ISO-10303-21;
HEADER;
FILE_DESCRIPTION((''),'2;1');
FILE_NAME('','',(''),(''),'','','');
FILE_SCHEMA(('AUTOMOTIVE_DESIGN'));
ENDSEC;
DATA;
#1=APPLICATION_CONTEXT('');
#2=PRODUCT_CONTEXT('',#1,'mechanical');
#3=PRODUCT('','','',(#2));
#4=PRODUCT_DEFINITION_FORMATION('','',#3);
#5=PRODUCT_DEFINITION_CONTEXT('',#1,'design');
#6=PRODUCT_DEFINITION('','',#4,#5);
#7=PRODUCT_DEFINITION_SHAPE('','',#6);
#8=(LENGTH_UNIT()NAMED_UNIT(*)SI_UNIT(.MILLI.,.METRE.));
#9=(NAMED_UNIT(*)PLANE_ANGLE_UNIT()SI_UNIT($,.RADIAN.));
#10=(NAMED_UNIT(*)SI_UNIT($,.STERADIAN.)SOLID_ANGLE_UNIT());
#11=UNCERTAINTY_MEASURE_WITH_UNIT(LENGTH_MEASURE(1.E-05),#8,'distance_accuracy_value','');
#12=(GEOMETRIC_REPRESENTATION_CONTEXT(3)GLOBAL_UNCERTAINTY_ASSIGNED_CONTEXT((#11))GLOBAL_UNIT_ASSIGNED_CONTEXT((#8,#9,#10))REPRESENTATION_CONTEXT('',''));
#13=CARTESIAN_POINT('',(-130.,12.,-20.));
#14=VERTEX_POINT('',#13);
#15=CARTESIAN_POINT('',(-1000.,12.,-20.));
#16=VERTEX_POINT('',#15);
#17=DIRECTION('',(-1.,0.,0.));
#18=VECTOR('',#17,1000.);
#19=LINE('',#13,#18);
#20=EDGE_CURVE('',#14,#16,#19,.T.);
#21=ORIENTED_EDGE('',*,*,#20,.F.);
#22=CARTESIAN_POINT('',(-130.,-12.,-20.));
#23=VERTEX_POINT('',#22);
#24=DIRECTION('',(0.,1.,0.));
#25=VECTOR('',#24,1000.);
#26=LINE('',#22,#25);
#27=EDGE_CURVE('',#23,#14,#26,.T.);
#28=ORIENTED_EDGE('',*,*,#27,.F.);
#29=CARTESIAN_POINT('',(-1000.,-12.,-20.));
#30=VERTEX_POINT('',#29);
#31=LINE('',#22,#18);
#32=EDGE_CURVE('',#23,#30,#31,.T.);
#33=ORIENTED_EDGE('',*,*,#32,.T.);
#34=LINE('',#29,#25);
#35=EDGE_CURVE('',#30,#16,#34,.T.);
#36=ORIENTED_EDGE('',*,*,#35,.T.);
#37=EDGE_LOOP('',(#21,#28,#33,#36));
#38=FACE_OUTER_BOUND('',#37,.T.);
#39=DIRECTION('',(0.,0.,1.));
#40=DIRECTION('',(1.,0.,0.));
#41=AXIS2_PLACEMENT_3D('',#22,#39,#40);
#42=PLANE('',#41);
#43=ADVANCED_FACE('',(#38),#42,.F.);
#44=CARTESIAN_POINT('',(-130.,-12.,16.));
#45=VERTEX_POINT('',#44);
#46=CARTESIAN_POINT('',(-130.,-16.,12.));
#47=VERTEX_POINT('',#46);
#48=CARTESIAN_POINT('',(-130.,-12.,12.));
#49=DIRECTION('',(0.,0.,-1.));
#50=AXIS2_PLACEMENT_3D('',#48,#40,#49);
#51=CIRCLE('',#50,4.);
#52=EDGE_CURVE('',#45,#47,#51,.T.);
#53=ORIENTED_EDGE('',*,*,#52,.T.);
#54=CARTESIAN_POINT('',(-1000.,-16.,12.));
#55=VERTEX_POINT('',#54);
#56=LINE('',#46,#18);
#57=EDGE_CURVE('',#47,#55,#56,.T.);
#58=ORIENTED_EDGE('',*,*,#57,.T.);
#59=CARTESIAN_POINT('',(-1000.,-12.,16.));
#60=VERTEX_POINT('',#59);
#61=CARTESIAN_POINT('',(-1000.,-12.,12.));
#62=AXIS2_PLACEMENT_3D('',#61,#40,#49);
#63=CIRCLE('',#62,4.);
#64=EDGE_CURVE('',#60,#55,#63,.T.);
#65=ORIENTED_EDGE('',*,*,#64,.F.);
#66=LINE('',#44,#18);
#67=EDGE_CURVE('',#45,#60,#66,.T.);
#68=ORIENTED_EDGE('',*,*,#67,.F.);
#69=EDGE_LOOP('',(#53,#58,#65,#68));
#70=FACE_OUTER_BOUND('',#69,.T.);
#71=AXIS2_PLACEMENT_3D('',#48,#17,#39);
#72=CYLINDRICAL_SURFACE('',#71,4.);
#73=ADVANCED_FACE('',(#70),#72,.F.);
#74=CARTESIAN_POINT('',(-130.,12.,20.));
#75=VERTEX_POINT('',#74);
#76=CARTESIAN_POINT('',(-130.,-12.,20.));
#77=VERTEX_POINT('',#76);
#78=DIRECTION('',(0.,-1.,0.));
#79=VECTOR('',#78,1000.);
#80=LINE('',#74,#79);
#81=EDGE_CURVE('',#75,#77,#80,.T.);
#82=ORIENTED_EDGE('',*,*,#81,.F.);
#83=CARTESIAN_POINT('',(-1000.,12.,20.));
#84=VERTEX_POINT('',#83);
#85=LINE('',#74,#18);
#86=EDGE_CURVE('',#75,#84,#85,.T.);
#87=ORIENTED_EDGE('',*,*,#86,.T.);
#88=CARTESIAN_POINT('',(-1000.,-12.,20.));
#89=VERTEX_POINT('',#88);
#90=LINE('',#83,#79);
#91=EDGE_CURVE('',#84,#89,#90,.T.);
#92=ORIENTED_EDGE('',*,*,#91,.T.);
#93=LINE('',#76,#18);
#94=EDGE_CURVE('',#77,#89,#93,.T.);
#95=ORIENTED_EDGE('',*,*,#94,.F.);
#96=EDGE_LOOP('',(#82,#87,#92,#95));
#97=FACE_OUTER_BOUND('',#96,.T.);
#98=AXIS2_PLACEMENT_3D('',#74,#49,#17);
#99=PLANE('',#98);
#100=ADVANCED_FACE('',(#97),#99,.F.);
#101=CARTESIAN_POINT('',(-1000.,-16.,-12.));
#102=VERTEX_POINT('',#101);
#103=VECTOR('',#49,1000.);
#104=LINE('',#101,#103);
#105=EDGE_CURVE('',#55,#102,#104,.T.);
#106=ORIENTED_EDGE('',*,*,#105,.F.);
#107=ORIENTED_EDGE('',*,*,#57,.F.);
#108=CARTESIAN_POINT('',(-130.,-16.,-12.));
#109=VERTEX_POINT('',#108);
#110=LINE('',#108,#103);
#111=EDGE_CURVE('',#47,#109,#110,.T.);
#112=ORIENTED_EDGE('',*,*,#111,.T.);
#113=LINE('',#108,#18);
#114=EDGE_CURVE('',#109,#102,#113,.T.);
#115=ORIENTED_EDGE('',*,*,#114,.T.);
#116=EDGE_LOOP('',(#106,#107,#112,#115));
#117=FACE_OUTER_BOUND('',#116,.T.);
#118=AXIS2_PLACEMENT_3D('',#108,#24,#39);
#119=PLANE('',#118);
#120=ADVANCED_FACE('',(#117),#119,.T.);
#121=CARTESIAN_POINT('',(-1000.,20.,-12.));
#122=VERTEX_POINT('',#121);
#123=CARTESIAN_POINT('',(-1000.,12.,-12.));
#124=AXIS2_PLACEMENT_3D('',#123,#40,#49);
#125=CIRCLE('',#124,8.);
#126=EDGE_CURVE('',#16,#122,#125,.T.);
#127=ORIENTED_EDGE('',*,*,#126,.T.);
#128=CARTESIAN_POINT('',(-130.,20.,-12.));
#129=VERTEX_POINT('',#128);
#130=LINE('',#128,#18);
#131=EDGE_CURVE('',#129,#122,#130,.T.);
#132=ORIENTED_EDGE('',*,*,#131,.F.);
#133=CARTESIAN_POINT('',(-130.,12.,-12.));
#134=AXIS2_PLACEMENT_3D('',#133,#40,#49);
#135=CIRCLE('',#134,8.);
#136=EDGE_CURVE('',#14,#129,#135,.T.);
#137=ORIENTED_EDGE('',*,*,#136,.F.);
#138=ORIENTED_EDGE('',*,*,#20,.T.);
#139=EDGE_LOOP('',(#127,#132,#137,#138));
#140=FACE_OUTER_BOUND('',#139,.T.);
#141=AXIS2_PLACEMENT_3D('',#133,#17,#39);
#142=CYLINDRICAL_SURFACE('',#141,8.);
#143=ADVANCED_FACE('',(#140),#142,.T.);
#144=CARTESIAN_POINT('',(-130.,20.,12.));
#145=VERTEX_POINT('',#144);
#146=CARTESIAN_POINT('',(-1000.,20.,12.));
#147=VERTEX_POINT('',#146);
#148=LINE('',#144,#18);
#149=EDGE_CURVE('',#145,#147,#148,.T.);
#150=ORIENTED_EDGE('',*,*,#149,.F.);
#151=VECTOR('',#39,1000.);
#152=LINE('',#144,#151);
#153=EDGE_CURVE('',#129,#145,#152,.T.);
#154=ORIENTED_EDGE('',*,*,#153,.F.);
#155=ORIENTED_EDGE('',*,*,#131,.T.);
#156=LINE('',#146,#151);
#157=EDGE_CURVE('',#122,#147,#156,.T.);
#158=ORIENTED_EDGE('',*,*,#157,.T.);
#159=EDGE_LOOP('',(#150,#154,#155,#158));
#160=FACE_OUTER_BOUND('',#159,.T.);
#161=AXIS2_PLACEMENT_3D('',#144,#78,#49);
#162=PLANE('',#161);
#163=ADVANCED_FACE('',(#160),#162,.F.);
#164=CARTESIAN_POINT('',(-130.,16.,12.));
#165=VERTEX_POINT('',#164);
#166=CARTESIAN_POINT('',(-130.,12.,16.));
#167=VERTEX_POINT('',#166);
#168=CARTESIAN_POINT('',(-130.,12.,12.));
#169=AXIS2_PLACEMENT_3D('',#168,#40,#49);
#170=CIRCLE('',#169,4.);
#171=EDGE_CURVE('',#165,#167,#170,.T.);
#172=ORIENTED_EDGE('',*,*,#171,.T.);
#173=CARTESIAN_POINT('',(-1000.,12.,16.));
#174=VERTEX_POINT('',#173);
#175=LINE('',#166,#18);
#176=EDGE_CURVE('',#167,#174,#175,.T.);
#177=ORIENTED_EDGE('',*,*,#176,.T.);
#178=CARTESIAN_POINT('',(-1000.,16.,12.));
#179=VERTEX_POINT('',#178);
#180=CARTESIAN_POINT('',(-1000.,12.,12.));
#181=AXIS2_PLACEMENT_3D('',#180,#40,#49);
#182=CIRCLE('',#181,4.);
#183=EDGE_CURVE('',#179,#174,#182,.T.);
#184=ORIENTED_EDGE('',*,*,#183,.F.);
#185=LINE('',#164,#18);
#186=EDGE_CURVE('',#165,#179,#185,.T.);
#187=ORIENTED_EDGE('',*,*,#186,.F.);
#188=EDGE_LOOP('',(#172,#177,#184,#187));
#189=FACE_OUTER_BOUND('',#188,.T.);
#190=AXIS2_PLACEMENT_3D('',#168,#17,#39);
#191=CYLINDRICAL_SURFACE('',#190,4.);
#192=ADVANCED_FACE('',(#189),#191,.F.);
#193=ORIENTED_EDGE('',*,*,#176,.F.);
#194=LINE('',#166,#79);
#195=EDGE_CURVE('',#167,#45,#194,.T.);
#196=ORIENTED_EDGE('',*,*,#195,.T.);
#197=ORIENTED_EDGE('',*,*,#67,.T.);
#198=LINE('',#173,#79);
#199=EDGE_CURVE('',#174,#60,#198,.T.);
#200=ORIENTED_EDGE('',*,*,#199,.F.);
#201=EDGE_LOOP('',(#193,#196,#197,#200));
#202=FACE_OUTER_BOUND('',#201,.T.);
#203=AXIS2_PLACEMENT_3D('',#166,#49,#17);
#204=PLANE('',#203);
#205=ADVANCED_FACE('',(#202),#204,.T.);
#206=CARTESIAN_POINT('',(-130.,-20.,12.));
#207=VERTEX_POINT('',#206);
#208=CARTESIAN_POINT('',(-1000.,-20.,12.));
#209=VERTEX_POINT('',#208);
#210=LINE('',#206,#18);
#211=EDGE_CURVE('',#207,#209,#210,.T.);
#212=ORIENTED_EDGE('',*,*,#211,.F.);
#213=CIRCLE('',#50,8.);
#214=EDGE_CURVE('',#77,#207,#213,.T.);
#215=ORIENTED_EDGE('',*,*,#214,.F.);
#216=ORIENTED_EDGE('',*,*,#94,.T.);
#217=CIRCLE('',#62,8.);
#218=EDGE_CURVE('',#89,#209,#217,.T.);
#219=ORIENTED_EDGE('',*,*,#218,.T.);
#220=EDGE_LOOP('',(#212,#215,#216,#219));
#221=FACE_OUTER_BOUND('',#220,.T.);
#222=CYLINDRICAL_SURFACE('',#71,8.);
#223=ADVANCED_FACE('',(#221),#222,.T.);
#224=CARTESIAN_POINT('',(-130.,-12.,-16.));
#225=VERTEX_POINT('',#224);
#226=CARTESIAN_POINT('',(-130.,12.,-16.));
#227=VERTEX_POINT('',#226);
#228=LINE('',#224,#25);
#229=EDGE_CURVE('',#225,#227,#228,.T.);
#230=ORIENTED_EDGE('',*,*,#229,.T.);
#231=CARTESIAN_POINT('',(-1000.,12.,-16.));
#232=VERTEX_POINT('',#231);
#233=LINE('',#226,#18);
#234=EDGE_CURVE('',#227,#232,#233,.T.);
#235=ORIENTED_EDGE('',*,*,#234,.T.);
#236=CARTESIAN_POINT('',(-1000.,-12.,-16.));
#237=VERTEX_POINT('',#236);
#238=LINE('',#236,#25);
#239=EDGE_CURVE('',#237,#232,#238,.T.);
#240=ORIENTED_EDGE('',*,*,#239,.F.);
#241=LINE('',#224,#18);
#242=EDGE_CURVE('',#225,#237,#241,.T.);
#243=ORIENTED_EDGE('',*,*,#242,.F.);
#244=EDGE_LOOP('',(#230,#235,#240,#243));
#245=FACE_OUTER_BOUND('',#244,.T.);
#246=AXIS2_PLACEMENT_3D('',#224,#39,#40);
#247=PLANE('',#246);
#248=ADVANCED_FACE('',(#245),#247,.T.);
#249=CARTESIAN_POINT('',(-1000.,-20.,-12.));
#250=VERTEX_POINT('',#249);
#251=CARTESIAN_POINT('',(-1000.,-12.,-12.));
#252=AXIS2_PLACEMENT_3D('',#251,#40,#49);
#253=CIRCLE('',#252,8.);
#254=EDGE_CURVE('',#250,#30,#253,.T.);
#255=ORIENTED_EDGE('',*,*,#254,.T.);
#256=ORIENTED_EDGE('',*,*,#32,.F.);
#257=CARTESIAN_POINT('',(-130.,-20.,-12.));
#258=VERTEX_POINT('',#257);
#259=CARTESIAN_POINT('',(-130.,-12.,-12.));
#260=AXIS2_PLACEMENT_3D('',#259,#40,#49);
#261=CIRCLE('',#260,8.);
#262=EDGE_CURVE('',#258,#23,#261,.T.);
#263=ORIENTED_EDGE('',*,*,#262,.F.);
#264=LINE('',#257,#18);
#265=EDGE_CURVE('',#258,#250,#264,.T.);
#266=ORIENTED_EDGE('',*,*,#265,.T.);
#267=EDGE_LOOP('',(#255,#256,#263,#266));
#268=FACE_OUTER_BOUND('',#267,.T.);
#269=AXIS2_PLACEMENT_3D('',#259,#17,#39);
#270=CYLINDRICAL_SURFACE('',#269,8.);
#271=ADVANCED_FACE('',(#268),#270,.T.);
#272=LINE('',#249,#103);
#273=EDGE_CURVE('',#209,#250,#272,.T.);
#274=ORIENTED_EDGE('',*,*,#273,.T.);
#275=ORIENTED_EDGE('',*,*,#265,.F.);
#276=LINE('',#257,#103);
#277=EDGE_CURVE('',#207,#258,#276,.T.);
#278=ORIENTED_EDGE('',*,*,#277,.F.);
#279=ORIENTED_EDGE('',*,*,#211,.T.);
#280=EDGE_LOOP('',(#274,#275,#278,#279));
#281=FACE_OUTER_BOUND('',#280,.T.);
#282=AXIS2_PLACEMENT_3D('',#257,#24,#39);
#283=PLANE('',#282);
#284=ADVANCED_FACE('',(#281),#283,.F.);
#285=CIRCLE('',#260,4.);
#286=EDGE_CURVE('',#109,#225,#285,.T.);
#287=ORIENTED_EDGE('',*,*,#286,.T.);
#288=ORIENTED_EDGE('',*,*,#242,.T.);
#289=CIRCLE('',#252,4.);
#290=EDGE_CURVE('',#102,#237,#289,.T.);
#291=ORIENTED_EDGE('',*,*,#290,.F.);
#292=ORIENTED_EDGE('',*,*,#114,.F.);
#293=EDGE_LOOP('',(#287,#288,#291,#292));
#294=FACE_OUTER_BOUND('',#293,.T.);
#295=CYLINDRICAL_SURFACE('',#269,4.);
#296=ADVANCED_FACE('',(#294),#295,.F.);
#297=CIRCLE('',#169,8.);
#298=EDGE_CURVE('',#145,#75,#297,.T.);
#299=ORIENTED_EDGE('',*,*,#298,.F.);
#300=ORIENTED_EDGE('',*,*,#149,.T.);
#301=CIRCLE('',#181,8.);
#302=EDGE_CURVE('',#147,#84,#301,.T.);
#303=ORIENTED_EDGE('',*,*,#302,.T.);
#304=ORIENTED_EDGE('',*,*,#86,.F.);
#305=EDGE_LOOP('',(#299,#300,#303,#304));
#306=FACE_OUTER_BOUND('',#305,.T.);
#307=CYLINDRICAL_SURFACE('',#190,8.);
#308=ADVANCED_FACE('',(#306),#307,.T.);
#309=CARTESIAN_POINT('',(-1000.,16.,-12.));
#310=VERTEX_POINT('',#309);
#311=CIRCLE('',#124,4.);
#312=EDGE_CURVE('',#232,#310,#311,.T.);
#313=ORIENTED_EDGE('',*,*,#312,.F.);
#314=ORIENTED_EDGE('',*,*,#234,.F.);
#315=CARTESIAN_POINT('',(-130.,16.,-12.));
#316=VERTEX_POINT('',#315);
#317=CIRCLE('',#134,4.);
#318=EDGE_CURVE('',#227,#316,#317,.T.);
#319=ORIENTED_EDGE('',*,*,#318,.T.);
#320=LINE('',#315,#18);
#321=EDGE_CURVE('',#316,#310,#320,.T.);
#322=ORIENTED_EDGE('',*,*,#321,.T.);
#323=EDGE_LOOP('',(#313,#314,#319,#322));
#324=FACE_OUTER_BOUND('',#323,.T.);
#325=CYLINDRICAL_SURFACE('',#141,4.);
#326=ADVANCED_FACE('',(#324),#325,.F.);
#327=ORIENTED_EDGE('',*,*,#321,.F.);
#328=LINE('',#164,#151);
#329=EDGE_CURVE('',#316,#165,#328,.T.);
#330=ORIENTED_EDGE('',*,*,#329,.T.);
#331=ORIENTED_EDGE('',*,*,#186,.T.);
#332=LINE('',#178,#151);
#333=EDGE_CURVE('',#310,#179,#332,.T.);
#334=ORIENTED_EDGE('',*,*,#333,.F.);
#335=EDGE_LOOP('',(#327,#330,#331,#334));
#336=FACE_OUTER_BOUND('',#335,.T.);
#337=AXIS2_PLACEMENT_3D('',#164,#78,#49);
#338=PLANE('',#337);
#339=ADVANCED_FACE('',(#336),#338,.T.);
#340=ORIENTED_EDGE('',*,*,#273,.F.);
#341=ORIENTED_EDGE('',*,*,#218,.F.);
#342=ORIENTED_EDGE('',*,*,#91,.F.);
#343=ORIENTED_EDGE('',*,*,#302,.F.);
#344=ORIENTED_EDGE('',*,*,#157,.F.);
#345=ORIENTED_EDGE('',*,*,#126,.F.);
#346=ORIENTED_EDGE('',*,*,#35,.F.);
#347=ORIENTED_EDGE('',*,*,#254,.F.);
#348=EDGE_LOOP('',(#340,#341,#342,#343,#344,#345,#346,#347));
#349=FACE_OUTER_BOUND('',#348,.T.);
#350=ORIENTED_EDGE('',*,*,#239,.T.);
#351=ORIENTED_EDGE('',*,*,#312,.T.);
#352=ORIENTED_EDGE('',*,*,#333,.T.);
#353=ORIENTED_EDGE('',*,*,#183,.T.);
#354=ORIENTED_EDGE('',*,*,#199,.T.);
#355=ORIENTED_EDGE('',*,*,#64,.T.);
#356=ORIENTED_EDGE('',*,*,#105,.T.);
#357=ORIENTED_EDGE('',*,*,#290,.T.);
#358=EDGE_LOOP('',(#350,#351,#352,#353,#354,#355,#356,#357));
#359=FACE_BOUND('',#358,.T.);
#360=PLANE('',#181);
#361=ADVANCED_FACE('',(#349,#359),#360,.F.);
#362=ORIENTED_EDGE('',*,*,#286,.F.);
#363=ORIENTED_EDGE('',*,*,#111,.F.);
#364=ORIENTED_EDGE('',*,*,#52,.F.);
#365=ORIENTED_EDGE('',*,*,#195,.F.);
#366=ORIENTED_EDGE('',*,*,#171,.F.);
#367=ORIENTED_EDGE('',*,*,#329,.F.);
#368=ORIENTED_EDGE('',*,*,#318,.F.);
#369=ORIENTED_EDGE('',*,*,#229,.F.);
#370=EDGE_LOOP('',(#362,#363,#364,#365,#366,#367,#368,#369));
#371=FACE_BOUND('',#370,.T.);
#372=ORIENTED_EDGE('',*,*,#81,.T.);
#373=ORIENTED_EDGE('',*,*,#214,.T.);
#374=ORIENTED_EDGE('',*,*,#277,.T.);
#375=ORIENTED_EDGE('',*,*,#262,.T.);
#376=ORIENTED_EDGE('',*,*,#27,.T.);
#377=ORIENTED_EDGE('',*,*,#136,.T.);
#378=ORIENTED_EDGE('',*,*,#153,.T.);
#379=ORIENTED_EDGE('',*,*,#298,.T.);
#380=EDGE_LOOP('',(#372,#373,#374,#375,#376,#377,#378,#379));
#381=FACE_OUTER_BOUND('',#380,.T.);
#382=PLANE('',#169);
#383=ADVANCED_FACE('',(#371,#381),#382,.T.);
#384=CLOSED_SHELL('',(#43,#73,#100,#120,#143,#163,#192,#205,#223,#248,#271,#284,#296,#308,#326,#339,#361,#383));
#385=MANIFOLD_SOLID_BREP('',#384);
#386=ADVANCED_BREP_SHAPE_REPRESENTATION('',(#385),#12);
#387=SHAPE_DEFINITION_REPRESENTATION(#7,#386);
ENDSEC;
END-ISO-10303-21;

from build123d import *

# Parameters (mm, degrees)
SQUARE_TUBE_40_X_40_X_4_1_DEPTH = 870


with BuildPart() as part:
    # Sketch1 → Square Tube 40 X 40 X 4(1) (new body)
    with BuildSketch(Plane.YZ.offset(-1000)):
        with BuildLine():
            Line((-12, -20), (12, -20))
            ThreePointArc((12, -20), (17.656854249, -17.656854249), (20, -12))
            Line((20, -12), (20, 12))
            ThreePointArc((20, 12), (17.656854249, 17.656854249), (12, 20))
            Line((12, 20), (-12, 20))
            ThreePointArc((-12, 20), (-17.656854249, 17.656854249), (-20, 12))
            Line((-20, 12), (-20, -12))
            ThreePointArc((-20, -12), (-17.656854249, -17.656854249), (-12, -20))
        make_face()
        with BuildLine():
            Line((-12, -16), (12, -16))
            ThreePointArc((12, -16), (14.828427125, -14.828427125), (16, -12))
            Line((16, -12), (16, 12))
            ThreePointArc((16, 12), (14.828427125, 14.828427125), (12, 16))
            Line((12, 16), (-12, 16))
            ThreePointArc((-12, 16), (-14.828427125, 14.828427125), (-16, 12))
            Line((-16, 12), (-16, -12))
            ThreePointArc((-16, -12), (-14.828427125, -14.828427125), (-12, -16))
        make_face(mode=Mode.SUBTRACT)
    extrude(amount=SQUARE_TUBE_40_X_40_X_4_1_DEPTH)


solid = part.part
